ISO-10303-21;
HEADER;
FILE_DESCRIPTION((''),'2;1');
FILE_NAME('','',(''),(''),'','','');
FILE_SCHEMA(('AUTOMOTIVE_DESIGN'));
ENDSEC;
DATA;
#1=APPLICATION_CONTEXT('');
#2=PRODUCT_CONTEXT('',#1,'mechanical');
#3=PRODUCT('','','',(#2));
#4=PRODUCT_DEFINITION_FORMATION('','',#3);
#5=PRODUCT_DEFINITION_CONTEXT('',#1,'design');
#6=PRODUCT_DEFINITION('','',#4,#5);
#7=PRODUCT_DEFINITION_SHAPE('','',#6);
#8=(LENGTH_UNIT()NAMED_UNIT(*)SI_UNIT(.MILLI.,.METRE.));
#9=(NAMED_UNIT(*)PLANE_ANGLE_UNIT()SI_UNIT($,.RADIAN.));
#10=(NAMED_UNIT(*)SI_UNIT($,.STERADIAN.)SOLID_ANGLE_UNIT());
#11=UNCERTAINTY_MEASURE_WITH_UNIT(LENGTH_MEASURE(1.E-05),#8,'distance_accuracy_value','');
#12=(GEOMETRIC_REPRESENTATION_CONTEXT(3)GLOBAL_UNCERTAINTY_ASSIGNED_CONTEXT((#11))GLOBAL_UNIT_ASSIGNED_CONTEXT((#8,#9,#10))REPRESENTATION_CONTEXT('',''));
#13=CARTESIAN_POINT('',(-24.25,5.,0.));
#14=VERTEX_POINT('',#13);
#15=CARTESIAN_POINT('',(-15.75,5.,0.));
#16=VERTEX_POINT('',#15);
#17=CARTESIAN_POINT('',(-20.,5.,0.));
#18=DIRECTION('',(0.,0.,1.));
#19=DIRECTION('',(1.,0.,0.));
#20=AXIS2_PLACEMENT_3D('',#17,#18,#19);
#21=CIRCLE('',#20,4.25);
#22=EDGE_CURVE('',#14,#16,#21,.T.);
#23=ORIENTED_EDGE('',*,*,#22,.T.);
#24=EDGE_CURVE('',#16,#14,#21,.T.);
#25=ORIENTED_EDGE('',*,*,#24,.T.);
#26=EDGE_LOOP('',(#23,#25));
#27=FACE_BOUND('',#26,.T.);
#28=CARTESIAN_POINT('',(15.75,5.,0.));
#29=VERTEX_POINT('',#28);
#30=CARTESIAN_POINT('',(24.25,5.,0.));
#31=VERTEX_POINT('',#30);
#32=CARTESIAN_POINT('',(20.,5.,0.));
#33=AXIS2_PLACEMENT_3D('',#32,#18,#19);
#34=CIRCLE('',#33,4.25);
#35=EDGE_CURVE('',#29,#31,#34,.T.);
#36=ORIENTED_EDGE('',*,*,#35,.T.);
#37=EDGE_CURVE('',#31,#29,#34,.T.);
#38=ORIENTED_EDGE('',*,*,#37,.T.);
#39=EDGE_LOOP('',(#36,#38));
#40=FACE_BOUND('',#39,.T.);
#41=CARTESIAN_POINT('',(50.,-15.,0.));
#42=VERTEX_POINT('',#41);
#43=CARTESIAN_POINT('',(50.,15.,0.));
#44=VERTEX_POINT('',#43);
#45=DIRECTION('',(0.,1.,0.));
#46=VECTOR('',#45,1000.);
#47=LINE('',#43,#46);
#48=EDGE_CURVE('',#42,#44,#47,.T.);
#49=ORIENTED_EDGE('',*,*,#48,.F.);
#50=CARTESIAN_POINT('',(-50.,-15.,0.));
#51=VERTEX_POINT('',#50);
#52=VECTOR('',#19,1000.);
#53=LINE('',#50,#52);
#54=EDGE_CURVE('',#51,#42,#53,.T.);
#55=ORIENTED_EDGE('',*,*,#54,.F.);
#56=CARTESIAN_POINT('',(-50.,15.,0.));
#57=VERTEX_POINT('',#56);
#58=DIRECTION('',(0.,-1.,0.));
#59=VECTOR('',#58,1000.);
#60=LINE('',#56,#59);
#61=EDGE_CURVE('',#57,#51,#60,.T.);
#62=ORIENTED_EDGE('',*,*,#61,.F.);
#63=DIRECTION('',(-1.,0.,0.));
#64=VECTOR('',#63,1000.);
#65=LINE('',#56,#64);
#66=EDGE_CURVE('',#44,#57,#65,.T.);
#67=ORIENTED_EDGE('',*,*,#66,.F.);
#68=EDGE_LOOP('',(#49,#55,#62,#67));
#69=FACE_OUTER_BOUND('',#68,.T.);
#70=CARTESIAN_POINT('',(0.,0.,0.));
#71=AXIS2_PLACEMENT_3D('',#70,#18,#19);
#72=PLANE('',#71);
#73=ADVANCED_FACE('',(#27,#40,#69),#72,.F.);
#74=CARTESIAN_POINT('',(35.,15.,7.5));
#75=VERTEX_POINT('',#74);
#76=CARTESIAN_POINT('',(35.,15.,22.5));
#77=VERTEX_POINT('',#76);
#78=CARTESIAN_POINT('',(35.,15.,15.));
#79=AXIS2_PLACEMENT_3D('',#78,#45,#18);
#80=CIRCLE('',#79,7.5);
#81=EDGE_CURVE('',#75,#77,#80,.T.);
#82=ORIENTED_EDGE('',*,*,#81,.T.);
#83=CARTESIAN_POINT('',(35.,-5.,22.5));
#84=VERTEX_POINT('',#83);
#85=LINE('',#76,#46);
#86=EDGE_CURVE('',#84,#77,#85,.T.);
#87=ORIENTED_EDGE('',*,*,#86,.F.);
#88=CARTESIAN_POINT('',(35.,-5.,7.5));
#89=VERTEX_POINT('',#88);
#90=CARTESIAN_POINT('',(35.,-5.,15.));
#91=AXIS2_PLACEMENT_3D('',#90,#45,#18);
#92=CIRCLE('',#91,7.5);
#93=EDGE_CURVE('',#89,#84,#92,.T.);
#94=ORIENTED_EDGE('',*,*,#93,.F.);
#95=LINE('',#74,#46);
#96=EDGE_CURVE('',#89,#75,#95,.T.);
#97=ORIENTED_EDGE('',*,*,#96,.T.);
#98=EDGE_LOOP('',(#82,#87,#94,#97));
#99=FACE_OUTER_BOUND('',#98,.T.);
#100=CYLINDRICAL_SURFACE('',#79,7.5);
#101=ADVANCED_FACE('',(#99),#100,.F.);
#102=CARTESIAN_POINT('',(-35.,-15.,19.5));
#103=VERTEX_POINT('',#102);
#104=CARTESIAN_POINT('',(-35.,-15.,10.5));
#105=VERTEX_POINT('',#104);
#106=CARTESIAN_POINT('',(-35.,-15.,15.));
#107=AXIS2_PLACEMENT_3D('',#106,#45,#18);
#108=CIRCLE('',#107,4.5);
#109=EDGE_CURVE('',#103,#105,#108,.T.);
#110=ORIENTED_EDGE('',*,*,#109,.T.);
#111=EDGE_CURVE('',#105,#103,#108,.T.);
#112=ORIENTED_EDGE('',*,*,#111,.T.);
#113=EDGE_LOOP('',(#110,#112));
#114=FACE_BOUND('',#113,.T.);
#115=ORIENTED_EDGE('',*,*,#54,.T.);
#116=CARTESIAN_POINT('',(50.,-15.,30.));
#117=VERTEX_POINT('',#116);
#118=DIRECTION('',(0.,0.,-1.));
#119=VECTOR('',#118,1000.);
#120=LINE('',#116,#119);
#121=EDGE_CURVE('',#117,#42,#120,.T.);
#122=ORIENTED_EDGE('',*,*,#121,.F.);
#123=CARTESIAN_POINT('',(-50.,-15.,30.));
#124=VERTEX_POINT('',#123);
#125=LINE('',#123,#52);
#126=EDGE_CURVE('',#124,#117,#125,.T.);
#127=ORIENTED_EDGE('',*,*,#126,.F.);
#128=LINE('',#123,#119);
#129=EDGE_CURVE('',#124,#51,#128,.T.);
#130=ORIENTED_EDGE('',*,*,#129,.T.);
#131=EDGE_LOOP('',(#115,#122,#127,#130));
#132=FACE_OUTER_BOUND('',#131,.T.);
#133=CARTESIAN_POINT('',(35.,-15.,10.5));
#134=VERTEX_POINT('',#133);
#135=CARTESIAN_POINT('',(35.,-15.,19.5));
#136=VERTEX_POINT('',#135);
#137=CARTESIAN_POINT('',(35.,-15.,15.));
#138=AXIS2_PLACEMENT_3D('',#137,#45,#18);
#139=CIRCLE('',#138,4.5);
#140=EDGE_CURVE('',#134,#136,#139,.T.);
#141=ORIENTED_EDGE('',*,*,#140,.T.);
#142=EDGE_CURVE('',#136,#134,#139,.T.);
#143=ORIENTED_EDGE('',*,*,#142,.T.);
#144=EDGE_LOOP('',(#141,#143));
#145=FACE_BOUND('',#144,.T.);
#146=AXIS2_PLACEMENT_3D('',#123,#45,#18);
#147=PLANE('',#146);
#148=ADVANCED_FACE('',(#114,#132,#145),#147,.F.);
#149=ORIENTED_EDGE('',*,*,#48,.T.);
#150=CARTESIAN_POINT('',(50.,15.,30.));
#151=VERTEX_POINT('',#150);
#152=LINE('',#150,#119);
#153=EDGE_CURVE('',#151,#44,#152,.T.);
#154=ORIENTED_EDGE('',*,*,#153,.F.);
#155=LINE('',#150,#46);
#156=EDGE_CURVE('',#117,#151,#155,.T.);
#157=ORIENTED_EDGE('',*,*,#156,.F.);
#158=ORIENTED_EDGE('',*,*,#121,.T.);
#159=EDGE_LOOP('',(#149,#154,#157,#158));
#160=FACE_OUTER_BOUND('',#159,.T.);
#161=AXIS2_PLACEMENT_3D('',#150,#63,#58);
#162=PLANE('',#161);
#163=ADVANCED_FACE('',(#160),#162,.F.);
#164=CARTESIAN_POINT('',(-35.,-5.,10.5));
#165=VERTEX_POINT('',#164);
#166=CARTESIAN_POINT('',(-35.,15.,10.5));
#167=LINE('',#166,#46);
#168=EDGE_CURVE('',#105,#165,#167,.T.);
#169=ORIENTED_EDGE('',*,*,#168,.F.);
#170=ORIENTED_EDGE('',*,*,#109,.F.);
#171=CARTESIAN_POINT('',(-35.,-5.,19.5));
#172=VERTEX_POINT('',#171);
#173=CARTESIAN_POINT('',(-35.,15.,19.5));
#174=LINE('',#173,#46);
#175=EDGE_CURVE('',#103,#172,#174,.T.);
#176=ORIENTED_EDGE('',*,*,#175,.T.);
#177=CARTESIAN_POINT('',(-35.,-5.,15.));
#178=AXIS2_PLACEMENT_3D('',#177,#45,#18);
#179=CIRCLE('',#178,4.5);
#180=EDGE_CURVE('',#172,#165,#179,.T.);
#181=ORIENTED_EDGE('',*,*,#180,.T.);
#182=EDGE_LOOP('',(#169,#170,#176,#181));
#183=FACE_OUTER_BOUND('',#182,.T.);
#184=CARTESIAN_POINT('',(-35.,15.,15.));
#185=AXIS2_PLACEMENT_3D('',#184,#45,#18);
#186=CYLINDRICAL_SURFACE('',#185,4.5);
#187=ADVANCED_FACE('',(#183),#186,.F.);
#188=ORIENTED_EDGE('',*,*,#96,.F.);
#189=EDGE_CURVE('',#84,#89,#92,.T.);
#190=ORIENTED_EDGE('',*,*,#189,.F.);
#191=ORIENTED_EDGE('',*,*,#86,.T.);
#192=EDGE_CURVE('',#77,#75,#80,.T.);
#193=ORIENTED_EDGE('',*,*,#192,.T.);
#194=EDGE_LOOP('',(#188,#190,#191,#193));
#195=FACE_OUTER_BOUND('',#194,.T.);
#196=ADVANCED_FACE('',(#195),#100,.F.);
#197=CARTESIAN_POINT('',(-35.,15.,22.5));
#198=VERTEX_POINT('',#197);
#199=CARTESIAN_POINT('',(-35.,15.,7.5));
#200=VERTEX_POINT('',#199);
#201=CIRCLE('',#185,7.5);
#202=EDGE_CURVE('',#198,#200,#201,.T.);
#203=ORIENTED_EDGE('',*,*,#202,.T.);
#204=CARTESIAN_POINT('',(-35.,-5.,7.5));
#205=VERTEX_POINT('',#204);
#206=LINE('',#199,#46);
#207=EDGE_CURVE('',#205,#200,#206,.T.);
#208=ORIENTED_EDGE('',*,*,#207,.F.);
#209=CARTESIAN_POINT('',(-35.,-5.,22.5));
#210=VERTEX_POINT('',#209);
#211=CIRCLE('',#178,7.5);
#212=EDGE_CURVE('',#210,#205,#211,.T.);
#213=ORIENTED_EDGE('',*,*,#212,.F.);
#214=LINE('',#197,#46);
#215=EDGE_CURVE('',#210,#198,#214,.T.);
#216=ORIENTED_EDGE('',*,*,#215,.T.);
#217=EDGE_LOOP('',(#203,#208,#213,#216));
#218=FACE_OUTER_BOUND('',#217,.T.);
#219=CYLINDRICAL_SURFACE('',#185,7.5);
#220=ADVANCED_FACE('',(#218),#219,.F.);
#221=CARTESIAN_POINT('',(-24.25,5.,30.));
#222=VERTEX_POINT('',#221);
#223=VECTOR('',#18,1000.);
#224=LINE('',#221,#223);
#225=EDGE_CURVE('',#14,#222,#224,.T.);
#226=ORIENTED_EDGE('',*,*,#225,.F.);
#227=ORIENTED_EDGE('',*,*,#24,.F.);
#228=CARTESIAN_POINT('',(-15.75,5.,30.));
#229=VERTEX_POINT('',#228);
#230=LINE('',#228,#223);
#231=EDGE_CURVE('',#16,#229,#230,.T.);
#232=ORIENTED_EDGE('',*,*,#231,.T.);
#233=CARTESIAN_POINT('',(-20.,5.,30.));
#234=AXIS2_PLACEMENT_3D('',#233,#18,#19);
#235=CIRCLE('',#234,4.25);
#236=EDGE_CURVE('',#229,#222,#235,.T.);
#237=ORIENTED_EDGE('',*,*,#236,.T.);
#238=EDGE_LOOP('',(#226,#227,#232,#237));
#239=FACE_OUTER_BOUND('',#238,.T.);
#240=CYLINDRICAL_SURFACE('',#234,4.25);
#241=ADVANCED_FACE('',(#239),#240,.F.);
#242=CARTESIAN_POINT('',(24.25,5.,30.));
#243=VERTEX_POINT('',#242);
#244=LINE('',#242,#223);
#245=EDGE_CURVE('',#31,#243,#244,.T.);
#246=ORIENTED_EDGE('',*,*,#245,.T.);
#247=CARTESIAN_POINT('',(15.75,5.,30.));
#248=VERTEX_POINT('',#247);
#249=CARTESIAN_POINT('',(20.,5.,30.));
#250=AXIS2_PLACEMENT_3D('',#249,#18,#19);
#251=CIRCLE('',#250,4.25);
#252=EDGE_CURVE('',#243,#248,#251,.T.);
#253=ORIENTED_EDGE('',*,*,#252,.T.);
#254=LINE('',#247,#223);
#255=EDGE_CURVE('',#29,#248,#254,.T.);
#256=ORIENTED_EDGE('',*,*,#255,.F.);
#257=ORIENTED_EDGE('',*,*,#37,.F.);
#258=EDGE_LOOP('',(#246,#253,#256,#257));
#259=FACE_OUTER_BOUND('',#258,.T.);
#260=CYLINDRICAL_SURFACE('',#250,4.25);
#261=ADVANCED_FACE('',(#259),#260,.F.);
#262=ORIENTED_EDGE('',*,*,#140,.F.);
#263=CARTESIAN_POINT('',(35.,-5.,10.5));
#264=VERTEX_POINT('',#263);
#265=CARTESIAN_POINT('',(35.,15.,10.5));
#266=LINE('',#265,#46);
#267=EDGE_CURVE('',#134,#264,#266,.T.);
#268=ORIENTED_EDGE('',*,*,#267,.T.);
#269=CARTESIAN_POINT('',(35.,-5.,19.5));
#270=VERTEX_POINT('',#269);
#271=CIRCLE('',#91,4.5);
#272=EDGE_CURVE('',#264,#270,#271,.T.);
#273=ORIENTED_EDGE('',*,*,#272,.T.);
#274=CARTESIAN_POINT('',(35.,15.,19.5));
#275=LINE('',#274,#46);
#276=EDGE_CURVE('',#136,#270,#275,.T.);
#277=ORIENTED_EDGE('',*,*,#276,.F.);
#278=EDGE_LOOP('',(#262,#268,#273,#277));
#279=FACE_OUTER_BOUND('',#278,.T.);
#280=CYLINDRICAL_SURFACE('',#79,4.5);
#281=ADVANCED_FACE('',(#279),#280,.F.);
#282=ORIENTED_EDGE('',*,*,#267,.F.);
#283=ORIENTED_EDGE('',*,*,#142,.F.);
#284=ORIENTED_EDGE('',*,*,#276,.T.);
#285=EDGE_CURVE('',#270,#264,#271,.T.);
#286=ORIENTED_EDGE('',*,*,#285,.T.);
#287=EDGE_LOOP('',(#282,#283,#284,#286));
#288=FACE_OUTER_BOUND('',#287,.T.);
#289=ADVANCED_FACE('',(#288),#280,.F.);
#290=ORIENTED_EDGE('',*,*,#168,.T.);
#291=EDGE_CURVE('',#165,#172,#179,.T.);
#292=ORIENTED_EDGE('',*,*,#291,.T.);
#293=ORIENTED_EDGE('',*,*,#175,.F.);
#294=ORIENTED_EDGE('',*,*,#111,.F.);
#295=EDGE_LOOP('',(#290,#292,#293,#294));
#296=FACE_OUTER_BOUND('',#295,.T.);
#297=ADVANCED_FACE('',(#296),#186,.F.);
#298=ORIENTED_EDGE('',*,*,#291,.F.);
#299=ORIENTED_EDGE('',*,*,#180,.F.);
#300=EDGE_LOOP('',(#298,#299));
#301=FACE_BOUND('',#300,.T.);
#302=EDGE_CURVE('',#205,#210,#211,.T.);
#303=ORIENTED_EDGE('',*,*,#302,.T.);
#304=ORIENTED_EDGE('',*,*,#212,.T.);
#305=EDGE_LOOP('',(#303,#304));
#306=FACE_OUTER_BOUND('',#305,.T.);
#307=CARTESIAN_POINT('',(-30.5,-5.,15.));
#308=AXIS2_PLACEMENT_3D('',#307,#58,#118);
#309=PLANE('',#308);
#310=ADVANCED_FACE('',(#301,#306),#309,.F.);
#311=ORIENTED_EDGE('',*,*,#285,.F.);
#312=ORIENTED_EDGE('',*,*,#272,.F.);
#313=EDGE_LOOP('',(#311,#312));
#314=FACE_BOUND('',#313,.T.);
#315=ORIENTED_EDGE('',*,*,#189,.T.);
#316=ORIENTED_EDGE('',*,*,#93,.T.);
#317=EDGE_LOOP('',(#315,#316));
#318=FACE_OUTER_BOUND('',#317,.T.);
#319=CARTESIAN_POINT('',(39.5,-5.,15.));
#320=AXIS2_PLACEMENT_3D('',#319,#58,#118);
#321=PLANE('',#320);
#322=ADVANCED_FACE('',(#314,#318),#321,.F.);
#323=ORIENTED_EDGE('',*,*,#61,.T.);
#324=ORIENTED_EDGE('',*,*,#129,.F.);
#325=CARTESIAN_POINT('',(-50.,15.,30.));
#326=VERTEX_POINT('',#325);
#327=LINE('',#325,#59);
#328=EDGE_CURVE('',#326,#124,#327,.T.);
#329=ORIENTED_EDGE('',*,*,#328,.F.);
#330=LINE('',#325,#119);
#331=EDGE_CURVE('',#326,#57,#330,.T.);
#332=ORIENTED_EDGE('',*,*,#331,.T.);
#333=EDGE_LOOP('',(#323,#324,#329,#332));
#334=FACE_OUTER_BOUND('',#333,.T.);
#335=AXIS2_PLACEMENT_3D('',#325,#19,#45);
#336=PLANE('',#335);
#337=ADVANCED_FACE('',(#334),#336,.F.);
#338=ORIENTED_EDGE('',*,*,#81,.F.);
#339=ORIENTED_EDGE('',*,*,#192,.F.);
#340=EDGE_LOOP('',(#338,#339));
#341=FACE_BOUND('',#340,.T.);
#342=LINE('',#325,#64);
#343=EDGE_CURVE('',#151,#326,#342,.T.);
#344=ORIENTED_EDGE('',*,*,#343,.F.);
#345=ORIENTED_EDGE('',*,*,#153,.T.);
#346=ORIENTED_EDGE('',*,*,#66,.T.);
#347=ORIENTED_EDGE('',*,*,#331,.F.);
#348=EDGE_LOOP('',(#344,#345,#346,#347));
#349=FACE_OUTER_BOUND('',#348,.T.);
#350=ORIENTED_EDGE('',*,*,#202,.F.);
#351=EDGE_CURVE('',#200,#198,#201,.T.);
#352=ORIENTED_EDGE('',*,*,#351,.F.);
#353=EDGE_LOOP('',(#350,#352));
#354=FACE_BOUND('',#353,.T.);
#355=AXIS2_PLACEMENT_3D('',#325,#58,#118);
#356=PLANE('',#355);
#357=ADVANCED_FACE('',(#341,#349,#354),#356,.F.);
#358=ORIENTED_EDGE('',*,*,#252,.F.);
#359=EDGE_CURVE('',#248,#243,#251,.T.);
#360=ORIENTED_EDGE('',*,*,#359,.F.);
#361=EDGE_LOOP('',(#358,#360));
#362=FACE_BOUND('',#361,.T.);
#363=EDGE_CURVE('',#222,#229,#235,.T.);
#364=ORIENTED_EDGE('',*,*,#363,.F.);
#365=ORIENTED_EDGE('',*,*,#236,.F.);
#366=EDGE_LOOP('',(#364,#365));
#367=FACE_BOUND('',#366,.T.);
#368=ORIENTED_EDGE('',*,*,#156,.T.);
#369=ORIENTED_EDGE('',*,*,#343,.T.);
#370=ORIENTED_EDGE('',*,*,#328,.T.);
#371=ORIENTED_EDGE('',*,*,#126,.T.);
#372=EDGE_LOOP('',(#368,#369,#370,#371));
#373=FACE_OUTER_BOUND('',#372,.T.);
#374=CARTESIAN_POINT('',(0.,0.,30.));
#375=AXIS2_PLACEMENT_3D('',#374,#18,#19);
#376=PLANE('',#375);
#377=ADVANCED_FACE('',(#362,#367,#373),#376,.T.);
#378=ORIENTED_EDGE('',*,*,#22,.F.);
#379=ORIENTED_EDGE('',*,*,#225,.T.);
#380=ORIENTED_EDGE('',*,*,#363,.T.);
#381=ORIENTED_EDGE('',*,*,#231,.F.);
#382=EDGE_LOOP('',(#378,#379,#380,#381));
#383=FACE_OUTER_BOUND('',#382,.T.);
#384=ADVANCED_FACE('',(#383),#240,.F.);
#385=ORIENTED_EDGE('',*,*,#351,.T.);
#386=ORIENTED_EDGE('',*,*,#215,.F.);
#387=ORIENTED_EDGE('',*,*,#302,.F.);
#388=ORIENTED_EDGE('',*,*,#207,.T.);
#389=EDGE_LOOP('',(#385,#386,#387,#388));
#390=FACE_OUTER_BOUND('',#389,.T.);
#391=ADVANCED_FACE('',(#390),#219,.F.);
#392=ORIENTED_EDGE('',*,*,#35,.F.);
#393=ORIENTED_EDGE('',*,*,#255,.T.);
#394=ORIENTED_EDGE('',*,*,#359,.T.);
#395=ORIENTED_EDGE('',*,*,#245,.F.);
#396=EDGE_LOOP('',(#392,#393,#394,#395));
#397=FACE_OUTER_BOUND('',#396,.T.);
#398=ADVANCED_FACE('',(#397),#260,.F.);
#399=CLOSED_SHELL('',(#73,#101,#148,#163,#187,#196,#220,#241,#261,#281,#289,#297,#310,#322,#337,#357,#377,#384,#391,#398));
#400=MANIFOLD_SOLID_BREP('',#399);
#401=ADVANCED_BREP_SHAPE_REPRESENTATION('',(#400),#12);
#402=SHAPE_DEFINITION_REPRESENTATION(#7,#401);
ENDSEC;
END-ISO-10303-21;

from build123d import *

# Parameters (mm, degrees)
SKETCH_1_W                = 100
SKETCH_1_H                = 30
EXTRUDE_1_DEPTH           = 30
HOLE_WIZARD_1_D           = 9
HOLE_WIZARD_1_CBORE_D     = 15
HOLE_WIZARD_1_CBORE_DEPTH = 20
HOLE_WIZARD_M10_1_D       = 8.5


with BuildPart() as part:
    # 草图1 → 凸台-拉伸1 (new body)
    with BuildSketch(Plane.XY):
        Rectangle(SKETCH_1_W, SKETCH_1_H)
    extrude(amount=EXTRUDE_1_DEPTH)

    # 打孔尺寸(%根据)内六角圆柱头螺钉的类型1 (through all)
    with Locations(Plane(origin=(0, 15, 0), x_dir=(1, 0, 0), z_dir=(0, 1, 0))):
        with Locations((-35, -15), (35, -15)):
            CounterBoreHole(HOLE_WIZARD_1_D / 2, HOLE_WIZARD_1_CBORE_D / 2, HOLE_WIZARD_1_CBORE_DEPTH)

    # M10 螺纹孔1 (through all)
    with Locations(Plane.XY.offset(30)):
        with Locations((-20, 5), (20, 5)):
            Hole(HOLE_WIZARD_M10_1_D / 2)


solid = part.part
